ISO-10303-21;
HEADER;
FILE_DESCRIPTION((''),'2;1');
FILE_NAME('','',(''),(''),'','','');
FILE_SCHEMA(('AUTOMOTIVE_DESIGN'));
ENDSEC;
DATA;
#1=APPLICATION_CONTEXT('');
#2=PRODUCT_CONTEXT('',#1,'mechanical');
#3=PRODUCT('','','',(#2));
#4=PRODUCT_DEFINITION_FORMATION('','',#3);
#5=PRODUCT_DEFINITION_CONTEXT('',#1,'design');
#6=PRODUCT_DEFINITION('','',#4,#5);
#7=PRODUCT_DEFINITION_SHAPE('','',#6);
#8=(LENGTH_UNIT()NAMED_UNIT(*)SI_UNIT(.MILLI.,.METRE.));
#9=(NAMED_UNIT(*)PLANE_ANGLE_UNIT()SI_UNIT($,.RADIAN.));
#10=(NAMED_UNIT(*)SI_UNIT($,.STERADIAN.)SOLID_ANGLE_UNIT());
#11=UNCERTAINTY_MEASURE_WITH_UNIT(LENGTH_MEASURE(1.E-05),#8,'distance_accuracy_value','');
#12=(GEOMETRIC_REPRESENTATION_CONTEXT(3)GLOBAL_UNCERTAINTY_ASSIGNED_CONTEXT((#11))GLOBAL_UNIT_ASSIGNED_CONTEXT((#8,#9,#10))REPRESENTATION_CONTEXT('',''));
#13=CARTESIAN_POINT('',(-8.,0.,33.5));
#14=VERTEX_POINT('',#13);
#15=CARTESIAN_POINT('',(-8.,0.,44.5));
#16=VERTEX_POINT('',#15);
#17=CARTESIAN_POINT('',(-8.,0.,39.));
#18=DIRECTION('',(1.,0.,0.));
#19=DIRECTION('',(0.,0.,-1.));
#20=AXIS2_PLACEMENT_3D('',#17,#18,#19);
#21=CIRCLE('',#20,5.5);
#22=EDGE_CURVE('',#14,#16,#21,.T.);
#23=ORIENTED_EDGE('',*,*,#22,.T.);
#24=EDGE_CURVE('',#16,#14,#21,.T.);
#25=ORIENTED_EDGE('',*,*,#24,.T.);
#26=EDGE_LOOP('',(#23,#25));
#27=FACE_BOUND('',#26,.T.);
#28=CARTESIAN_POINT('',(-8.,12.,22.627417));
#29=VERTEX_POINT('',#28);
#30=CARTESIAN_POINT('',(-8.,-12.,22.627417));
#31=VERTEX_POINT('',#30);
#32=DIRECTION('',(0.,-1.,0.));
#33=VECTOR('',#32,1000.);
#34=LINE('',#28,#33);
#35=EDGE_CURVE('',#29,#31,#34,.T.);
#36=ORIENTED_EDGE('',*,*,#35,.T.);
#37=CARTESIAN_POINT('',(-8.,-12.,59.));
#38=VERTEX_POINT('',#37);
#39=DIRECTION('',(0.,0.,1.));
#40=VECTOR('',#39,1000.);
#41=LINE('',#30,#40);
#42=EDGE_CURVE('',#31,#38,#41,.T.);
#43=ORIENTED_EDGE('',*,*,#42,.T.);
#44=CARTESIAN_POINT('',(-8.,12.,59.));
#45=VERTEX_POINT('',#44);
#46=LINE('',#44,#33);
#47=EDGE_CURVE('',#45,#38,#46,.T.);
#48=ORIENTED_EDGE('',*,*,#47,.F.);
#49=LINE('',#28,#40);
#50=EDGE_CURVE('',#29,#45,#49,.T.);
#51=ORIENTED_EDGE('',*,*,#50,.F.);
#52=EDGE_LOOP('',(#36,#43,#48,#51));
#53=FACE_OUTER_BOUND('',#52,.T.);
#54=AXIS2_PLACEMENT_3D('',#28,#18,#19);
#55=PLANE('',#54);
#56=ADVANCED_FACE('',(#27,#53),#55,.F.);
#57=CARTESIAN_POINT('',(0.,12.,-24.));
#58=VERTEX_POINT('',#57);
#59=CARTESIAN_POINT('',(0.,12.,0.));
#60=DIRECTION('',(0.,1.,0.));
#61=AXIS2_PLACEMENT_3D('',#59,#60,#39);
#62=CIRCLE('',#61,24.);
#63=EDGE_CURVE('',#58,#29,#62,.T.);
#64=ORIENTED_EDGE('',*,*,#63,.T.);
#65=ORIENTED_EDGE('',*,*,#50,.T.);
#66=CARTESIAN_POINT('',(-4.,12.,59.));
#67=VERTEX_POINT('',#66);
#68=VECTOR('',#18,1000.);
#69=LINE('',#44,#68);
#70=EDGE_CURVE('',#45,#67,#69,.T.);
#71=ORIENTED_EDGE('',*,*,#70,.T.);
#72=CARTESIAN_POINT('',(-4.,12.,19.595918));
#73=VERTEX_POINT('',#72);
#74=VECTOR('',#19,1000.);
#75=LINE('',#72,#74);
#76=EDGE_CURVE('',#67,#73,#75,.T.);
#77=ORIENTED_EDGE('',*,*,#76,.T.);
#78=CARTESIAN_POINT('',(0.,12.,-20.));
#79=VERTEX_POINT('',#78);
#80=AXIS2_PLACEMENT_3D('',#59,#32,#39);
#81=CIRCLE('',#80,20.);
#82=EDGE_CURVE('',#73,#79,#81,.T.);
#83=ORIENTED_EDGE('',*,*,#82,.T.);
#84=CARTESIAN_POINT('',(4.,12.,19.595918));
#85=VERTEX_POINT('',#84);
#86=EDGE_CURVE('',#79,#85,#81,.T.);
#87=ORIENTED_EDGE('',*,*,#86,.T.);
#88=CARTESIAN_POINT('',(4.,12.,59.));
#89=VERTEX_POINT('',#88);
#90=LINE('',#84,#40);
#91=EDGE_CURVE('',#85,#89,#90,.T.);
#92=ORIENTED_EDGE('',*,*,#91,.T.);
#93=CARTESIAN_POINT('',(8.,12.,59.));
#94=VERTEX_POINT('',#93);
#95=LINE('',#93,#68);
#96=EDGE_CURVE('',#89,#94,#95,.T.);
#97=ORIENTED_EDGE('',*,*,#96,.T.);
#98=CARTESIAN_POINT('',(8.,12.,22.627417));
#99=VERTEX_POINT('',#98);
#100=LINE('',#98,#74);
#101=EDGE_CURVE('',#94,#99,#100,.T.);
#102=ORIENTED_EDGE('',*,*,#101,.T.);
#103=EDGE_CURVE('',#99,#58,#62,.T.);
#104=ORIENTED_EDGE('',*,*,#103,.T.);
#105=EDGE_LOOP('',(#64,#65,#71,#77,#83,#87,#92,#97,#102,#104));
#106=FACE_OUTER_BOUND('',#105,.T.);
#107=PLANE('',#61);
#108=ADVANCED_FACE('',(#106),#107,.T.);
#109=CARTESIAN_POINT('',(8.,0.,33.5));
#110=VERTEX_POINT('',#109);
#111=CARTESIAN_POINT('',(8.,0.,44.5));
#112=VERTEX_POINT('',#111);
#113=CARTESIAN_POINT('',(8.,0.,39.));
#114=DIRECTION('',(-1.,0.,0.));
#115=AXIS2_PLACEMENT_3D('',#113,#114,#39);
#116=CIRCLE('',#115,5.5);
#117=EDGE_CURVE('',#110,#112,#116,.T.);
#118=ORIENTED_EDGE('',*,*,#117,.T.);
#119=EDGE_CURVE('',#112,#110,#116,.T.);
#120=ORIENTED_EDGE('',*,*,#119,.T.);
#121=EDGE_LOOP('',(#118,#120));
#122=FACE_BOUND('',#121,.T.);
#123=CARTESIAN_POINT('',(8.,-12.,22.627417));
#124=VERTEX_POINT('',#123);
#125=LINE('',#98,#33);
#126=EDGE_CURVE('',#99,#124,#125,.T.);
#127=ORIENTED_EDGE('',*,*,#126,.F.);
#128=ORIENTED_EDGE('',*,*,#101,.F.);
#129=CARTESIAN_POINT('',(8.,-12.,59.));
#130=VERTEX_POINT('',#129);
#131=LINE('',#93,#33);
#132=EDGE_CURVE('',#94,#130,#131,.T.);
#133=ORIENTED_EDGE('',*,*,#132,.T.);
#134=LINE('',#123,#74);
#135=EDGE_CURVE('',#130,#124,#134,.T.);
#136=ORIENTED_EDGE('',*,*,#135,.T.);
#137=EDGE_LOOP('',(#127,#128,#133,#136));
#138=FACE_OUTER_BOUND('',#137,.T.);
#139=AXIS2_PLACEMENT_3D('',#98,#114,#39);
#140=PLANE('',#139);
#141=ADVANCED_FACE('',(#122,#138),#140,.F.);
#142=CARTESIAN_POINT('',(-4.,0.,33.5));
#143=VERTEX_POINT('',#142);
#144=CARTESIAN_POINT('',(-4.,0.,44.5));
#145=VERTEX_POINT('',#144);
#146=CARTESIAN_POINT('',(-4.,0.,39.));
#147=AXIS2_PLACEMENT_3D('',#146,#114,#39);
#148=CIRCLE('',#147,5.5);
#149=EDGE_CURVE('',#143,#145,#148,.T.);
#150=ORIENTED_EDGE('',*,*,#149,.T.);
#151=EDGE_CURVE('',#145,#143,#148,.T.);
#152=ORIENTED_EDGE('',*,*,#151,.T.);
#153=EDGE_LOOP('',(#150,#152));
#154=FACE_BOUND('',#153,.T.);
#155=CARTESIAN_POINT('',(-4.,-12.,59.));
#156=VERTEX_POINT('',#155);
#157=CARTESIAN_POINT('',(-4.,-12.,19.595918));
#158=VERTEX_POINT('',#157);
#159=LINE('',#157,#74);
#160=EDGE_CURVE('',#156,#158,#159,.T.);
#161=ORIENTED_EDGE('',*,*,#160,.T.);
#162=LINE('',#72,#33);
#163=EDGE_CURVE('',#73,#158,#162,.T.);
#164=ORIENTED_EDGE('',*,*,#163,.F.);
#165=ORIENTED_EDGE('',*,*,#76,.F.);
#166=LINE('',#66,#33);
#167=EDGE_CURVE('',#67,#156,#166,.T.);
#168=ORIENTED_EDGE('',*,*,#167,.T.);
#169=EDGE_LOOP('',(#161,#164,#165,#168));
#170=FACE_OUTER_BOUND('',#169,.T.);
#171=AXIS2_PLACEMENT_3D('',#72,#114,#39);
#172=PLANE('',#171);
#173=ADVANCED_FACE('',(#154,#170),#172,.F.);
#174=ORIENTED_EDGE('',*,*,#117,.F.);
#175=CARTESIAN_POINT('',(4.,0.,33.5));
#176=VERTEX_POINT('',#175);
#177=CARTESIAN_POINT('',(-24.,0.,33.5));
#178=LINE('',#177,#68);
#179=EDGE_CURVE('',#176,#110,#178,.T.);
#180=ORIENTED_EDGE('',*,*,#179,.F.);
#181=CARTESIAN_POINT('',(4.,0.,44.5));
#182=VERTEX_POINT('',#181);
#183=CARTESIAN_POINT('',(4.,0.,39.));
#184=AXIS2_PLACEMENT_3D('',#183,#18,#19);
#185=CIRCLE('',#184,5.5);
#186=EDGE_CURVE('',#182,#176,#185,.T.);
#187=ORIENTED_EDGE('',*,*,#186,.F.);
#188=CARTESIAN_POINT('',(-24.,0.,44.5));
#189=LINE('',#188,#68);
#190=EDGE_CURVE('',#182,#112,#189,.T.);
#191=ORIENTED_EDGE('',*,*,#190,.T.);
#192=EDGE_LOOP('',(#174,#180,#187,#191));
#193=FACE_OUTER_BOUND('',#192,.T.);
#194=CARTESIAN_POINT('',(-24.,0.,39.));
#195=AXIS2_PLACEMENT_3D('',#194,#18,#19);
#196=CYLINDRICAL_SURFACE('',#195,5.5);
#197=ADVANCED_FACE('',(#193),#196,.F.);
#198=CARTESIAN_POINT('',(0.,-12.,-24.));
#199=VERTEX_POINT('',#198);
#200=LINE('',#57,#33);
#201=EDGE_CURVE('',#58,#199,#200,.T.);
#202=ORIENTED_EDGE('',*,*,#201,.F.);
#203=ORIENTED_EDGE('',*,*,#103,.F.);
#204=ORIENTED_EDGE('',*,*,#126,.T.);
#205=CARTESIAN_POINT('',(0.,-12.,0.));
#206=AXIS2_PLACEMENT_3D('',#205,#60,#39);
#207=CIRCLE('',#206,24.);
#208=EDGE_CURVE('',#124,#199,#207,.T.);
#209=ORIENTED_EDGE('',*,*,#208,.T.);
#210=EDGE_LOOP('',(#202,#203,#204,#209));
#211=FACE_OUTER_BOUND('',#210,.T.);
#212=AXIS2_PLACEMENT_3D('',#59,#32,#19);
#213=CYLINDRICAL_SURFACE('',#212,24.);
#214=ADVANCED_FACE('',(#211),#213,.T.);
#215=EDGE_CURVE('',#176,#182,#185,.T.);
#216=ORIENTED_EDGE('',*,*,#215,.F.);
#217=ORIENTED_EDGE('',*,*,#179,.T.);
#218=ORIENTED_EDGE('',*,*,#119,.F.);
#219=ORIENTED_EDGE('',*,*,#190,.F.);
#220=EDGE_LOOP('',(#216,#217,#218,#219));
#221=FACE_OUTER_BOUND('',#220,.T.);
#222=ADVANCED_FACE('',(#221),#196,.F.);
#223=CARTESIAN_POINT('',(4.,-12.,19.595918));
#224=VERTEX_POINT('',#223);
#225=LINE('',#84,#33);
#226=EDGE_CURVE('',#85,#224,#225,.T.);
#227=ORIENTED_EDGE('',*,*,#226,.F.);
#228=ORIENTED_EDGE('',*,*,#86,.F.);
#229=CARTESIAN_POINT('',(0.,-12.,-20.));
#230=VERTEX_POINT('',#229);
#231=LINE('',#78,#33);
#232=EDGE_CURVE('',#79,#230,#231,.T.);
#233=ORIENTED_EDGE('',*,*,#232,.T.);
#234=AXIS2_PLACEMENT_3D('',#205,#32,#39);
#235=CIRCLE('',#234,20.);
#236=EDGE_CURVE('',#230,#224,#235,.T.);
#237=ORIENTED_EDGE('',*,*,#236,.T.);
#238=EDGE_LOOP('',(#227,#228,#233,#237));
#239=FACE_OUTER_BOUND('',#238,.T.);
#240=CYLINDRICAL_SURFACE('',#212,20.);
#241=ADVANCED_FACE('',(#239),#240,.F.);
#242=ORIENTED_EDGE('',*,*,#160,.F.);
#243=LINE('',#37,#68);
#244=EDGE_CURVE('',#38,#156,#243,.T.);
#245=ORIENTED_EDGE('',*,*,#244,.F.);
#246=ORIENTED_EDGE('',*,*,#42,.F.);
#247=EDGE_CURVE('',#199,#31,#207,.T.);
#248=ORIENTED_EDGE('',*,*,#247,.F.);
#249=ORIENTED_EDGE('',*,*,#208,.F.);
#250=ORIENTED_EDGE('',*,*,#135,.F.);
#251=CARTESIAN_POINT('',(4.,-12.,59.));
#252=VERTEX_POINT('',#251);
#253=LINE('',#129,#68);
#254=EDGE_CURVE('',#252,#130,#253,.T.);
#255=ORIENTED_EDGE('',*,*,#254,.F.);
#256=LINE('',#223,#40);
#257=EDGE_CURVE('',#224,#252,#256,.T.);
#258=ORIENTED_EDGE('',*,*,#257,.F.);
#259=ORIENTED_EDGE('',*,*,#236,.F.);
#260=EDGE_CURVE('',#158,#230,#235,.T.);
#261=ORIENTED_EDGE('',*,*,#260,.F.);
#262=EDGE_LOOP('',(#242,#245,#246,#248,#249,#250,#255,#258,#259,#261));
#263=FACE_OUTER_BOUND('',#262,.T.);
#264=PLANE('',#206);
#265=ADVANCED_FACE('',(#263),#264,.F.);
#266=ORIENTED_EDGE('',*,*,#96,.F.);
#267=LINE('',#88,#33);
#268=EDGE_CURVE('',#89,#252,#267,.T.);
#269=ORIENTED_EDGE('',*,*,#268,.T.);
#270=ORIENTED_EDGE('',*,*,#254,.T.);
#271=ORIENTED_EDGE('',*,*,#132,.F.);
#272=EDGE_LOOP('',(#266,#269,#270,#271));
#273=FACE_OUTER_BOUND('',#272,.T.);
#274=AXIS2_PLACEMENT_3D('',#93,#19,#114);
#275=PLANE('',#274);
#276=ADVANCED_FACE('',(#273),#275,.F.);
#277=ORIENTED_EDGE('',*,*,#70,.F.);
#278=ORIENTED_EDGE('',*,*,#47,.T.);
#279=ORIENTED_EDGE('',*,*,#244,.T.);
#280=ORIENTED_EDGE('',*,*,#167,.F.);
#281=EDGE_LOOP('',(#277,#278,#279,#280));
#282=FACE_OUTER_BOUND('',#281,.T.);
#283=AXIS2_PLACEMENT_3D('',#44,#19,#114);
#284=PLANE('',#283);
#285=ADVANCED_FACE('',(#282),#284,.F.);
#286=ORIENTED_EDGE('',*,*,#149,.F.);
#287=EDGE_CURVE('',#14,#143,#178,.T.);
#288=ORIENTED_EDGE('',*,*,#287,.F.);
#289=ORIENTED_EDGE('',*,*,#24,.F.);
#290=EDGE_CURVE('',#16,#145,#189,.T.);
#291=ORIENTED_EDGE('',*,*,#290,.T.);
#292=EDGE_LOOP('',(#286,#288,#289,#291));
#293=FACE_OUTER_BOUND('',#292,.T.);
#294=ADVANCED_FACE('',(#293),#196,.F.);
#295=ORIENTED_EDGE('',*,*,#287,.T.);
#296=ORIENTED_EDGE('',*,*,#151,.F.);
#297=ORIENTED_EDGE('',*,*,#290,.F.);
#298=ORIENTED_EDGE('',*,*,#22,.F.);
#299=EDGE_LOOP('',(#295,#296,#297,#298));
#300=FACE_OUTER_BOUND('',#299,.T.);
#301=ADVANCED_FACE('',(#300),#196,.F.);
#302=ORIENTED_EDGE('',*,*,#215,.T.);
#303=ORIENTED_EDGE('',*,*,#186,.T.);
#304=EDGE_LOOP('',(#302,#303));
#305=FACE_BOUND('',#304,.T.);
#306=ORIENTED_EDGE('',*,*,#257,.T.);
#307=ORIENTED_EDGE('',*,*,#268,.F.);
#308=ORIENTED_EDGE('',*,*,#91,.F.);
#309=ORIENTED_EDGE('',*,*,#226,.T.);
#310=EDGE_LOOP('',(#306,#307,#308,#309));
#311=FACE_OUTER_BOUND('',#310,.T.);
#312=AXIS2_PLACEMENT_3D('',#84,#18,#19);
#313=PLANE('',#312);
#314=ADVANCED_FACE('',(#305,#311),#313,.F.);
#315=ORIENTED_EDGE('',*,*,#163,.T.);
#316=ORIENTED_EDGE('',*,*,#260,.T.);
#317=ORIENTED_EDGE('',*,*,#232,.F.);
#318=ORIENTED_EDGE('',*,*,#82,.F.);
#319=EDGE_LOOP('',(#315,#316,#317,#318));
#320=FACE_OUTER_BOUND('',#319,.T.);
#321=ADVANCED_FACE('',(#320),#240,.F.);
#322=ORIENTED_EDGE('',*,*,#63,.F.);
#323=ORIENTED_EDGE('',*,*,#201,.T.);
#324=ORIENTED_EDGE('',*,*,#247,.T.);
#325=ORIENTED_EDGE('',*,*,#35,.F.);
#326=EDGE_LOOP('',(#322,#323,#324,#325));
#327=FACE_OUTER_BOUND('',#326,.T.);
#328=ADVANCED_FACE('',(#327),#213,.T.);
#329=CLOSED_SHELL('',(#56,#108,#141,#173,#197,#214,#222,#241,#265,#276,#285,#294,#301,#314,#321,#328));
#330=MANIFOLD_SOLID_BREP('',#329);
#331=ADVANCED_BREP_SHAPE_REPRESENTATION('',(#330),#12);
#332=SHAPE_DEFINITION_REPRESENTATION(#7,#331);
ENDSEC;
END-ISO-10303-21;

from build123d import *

# Parameters (mm, degrees)
EXTRUDE_1_DEPTH          = 12
CUT_EXTRUDE_1_DEPTH      = 65.815121692
CUT_EXTRUDE_1_DEPTH_BACK = 65.815121692
SKETCH_2_R               = 5.5


with BuildPart() as part:
    # 草图1 → 凸台-拉伸1 (new, symmetric)
    with BuildSketch(Plane(origin=(0, 0, 0), x_dir=(1, 0, 0), z_dir=(0, 1, 0))):
        with BuildLine():
            Line((8, -59), (4, -59))
            Line((4, -59), (4, -19.595917942))
            ThreePointArc((4, -19.595917942), (0, 20), (-4, -19.595917942))
            Line((-4, -19.595917942), (-4, -59))
            Line((-4, -59), (-8, -59))
            Line((-8, -59), (-8, -22.627416998))
            ThreePointArc((-8, -22.627416998), (0, 24), (8, -22.627416998))
            Line((8, -22.627416998), (8, -59))
        make_face()
    extrude(amount=EXTRUDE_1_DEPTH, both=True)

    # 草图2 → 切除-拉伸1 (cut, two sides: drawn at the far end of the back side and taken through both)
    with BuildSketch(Plane(origin=(0, 0, 0), x_dir=(0, 0, -1), z_dir=(1, 0, 0)).offset(-CUT_EXTRUDE_1_DEPTH_BACK)):
        with Locations((-39, 0)):
            Circle(SKETCH_2_R)
    extrude(amount=CUT_EXTRUDE_1_DEPTH + CUT_EXTRUDE_1_DEPTH_BACK, mode=Mode.SUBTRACT)


solid = part.part
